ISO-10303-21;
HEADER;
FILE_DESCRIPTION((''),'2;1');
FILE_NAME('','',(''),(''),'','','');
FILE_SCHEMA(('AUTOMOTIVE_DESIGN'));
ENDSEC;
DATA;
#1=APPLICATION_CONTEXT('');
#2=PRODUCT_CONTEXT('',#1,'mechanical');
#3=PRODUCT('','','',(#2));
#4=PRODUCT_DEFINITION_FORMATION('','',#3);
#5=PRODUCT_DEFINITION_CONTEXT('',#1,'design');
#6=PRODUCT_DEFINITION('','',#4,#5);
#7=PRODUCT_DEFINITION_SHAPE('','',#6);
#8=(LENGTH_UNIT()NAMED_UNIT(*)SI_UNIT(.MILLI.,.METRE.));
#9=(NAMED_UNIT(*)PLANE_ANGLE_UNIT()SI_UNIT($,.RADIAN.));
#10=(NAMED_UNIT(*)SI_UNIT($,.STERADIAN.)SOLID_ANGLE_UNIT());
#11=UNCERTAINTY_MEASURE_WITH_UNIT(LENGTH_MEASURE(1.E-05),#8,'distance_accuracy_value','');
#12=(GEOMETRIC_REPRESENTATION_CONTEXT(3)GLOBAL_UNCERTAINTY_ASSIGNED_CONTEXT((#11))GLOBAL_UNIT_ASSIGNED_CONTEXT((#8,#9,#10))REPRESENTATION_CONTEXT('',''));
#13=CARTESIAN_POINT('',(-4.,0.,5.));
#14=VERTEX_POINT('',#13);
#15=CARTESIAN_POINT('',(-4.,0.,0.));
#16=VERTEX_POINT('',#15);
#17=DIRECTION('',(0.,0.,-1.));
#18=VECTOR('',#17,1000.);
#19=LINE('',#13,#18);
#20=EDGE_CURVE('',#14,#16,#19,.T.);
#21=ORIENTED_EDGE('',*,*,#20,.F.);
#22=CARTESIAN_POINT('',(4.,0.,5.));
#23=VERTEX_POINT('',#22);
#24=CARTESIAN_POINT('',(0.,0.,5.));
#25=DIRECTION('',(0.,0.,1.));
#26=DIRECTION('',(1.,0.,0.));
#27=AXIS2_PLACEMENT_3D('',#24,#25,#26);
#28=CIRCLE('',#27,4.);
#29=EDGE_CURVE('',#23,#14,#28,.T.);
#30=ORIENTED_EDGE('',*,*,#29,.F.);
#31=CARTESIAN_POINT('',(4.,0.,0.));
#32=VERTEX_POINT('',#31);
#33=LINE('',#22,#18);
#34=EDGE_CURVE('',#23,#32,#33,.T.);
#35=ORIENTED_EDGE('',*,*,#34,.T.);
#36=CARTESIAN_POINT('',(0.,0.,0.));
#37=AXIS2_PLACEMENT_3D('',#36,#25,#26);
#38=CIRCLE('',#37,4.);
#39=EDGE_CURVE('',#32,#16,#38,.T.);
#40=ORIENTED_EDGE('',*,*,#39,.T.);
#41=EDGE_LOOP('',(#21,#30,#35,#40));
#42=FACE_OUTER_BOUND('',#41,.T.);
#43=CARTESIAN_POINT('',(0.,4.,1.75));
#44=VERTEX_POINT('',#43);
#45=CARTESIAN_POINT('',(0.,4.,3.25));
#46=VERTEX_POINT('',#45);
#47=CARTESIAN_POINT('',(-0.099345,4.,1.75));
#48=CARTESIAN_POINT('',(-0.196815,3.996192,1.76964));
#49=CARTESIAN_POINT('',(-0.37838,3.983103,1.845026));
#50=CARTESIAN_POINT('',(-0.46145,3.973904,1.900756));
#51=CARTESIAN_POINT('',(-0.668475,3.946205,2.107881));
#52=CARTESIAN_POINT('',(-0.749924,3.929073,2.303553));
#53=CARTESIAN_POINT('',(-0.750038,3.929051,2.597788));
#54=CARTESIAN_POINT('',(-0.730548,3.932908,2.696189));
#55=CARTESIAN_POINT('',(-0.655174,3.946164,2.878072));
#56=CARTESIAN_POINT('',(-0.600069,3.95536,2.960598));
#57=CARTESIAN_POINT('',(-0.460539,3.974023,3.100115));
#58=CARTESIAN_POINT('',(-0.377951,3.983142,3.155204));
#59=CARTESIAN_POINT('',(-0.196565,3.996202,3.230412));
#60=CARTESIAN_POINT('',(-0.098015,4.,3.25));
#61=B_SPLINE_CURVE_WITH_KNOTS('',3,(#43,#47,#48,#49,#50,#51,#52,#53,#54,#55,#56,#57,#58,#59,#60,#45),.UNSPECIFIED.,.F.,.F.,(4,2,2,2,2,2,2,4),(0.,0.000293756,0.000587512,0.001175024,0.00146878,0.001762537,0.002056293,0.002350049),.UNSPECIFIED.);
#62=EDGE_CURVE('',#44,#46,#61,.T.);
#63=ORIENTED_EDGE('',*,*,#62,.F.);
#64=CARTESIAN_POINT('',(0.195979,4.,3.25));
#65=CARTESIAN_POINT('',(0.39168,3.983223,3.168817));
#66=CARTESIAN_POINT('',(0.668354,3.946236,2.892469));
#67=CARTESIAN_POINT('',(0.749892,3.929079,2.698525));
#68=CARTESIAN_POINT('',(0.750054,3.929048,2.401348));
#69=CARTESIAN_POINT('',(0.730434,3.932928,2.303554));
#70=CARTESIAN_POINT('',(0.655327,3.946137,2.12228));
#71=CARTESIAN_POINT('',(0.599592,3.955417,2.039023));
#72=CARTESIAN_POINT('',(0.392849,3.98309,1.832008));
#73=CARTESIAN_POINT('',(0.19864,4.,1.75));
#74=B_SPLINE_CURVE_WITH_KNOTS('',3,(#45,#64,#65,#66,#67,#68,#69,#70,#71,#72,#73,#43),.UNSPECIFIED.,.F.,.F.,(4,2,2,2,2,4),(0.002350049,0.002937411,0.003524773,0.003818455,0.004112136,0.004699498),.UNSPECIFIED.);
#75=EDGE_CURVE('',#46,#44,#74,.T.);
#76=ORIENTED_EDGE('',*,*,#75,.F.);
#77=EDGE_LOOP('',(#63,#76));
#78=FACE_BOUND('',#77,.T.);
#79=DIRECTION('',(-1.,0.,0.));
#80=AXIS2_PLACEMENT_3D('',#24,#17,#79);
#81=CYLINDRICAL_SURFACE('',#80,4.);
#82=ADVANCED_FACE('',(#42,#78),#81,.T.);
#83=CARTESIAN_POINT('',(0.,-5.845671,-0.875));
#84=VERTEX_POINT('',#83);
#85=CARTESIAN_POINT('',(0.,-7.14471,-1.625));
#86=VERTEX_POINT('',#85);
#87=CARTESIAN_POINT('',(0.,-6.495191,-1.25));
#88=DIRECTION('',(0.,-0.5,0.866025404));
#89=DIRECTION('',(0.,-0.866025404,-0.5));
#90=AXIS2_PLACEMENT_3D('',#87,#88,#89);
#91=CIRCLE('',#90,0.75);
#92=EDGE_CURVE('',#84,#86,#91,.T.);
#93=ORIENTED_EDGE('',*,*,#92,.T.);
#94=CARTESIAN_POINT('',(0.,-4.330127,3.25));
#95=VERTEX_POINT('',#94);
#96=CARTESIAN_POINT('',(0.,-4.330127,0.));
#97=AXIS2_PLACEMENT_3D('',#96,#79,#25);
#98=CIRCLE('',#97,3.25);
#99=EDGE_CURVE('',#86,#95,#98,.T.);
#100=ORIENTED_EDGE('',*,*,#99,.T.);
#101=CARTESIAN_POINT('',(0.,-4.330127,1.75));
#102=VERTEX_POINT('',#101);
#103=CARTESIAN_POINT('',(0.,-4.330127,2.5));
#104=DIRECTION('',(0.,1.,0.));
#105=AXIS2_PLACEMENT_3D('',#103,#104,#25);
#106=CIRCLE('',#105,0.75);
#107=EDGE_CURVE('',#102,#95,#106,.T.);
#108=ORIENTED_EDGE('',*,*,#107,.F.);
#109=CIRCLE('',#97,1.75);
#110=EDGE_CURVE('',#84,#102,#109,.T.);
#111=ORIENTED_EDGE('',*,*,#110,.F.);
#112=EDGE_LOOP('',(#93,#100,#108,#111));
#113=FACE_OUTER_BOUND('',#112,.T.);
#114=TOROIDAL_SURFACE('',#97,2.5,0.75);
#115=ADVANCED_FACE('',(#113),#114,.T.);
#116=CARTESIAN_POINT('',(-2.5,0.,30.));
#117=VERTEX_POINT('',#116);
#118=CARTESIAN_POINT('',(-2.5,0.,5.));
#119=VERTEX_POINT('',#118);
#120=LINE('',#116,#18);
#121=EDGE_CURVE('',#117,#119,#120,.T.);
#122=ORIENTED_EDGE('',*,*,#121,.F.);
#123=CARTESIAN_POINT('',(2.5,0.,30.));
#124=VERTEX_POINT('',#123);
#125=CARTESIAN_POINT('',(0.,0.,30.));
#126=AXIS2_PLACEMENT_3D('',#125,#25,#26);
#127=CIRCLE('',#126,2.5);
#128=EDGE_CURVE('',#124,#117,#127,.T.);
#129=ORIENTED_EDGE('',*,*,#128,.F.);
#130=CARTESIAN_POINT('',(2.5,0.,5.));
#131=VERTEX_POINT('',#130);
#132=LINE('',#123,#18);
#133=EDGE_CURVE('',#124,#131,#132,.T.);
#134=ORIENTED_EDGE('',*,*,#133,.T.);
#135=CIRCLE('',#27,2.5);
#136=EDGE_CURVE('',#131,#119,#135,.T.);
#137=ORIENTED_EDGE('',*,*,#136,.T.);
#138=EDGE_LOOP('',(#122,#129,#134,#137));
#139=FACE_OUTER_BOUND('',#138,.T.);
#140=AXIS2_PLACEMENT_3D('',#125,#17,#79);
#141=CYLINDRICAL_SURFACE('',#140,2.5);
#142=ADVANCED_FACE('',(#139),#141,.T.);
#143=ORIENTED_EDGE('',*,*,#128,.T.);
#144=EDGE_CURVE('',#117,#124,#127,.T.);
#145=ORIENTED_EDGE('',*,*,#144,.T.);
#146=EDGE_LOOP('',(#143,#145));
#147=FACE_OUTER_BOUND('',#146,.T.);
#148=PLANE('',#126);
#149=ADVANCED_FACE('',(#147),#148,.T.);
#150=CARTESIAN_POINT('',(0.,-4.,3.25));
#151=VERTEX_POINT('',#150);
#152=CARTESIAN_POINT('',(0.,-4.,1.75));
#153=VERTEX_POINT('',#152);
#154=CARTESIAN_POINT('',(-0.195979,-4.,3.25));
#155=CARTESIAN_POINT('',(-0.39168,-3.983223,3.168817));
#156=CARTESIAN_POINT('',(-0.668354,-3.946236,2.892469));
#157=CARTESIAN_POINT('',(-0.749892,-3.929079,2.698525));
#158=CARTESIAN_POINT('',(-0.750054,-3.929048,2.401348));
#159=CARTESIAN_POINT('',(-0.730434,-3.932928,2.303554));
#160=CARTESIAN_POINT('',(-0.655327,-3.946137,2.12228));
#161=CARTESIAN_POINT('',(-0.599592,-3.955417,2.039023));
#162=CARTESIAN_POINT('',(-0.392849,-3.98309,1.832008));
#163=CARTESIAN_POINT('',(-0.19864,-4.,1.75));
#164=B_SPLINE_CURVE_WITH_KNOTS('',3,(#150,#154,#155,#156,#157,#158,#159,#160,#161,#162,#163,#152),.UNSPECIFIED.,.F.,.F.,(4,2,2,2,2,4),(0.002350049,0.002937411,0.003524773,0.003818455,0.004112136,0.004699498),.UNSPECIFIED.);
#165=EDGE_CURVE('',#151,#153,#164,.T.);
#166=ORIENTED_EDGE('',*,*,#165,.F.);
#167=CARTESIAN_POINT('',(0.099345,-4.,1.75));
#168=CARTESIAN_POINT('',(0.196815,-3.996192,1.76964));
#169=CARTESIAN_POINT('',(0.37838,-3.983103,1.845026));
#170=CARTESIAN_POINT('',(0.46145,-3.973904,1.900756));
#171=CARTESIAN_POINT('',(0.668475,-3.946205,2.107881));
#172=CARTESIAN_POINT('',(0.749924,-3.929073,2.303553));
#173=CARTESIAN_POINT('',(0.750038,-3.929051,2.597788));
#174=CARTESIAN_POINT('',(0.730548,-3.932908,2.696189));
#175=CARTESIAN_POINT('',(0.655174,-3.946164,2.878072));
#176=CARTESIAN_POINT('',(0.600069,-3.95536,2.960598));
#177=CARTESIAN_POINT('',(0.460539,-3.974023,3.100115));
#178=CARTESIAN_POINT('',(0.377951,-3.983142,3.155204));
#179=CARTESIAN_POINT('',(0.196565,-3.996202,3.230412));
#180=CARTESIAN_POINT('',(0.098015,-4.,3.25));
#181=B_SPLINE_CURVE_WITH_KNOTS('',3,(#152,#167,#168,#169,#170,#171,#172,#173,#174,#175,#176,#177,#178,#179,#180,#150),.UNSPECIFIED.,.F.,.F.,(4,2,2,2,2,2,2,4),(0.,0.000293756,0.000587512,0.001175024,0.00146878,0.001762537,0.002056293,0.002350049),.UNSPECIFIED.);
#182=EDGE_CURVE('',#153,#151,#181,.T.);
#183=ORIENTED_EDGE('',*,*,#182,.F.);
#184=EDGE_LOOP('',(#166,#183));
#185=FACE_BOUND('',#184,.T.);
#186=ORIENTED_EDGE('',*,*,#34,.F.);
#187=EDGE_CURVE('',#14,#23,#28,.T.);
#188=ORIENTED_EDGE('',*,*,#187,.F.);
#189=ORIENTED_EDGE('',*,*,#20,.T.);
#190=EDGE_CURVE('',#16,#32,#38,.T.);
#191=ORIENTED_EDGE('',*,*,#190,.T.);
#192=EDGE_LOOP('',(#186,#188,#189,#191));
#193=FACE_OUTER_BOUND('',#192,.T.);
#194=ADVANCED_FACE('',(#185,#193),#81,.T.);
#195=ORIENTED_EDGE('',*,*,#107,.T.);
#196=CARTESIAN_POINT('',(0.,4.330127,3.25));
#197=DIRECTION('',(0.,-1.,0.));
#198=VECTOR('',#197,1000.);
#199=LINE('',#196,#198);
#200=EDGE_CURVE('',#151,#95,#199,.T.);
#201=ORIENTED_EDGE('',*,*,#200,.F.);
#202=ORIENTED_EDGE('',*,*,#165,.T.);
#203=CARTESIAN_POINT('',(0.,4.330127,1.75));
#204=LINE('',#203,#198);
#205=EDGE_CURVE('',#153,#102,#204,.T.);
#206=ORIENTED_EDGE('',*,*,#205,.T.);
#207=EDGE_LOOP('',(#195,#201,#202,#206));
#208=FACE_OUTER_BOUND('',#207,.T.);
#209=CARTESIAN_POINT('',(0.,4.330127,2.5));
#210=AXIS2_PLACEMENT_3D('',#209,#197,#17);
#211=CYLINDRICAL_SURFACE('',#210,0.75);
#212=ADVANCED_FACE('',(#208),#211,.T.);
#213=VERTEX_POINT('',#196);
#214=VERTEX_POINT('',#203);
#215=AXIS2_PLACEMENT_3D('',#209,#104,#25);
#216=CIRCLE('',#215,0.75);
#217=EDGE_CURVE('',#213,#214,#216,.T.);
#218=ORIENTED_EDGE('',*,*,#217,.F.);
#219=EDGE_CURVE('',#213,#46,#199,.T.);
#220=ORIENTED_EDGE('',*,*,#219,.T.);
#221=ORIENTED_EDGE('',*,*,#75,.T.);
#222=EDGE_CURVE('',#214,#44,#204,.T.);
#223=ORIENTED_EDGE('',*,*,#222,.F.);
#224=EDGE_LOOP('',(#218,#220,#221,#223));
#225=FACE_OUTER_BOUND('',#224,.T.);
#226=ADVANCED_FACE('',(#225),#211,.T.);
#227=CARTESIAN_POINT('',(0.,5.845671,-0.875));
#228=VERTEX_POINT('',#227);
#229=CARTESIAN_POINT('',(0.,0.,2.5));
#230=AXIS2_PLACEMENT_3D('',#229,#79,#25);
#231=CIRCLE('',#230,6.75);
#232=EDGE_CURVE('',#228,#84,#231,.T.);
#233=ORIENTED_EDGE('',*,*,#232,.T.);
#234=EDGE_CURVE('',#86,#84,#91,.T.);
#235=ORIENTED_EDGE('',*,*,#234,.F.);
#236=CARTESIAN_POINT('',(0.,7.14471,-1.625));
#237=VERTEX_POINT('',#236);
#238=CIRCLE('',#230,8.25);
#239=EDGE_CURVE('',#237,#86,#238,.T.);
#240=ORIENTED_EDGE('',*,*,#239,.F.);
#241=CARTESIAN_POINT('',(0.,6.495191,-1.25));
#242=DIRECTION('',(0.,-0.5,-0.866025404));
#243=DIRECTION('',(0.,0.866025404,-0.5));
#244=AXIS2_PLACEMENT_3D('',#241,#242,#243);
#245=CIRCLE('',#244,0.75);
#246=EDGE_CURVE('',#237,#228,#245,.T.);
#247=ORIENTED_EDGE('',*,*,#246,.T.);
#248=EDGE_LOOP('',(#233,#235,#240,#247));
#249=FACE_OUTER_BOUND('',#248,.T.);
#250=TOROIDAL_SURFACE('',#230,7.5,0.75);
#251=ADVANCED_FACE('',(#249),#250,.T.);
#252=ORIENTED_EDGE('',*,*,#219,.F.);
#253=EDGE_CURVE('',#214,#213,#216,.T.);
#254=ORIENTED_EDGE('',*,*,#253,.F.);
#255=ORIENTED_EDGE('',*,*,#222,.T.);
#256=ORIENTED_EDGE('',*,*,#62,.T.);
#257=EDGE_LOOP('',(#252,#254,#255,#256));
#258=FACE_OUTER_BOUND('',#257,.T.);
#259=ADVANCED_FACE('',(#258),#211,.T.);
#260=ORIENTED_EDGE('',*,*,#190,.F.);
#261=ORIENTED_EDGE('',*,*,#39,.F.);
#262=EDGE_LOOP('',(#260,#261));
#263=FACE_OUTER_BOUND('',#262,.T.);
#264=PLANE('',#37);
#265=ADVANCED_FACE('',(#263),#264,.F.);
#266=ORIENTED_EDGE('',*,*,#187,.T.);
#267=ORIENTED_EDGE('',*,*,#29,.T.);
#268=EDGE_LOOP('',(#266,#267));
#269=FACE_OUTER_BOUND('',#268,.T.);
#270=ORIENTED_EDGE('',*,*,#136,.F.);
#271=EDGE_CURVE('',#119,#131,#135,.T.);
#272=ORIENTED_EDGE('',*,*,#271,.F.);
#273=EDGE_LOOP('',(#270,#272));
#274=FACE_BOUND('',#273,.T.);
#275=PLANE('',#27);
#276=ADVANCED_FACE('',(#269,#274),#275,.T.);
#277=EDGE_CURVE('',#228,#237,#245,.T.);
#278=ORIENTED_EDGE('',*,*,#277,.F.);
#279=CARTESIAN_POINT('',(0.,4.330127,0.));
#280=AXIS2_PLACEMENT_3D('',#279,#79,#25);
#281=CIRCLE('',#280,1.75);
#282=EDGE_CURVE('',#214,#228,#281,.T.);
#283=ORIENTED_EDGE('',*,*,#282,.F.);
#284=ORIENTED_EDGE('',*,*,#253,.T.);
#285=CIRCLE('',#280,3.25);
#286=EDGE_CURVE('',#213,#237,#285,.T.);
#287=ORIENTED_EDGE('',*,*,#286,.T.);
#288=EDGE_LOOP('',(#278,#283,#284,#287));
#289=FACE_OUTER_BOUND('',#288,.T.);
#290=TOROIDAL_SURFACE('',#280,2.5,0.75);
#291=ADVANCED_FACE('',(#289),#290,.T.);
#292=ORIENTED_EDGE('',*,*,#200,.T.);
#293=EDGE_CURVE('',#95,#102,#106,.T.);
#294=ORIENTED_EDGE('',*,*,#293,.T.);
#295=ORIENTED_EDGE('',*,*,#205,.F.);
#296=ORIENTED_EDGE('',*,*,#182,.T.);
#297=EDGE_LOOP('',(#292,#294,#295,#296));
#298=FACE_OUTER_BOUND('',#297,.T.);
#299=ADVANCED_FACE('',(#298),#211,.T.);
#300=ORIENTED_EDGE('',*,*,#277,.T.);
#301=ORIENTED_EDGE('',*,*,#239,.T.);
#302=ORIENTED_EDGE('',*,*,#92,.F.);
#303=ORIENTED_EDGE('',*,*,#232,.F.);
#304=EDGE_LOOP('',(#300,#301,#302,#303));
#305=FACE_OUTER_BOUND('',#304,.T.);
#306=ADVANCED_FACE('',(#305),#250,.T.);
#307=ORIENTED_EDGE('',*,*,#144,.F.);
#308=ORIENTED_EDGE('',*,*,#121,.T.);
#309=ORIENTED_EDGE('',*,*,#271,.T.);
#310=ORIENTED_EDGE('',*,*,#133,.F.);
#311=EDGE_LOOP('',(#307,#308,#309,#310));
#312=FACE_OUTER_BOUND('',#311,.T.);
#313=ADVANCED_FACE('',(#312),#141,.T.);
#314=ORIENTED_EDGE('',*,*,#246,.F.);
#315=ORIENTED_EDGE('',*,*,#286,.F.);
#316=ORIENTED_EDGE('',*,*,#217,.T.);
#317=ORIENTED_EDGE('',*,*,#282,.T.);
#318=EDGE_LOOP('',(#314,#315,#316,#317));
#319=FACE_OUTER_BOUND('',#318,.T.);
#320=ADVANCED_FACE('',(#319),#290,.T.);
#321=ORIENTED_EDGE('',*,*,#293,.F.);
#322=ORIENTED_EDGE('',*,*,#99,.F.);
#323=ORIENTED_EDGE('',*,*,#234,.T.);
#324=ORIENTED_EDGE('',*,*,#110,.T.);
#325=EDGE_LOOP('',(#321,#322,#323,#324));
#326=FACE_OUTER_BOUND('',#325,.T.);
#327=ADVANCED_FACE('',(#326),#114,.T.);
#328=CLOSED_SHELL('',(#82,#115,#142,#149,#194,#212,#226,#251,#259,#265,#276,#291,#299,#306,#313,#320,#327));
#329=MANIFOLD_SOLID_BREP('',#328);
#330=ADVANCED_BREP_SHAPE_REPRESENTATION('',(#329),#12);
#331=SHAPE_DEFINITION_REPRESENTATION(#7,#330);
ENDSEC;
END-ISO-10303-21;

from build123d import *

# Parameters (mm, degrees)
SKETCH1_R           = 4
BOSS_EXTRUDE1_DEPTH = 5
SKETCH2_R           = 2.5
BOSS_EXTRUDE2_DEPTH = 25
SKETCH3_R           = 0.75


with BuildPart() as part:
    # Sketch1 → Boss-Extrude1 (new body)
    with BuildSketch(Plane.XY):
        Circle(SKETCH1_R)
    extrude(amount=BOSS_EXTRUDE1_DEPTH)

    # Sketch2 → Boss-Extrude2 (add)
    with BuildSketch(Plane.XY.offset(5)):
        Circle(SKETCH2_R)
    extrude(amount=BOSS_EXTRUDE2_DEPTH)

    # Sweep1: sweep along a path in Sketch4
    with BuildLine(Plane(origin=(0, 0, 0), x_dir=(0, 0, -1), z_dir=(1, 0, 0))) as sweep1_path:
        Line((-2.5, 0), (-2.5, -4.330127019))
        ThreePointArc((-2.5, -4.330127019), (-1.25, -6.495190528), (1.25, -6.495190528))
        ThreePointArc((1.25, -6.495190528), (5, 0), (1.25, 6.495190528))
        ThreePointArc((1.25, 6.495190528), (-1.25, 6.495190528), (-2.5, 4.330127019))
        Line((-2.5, 4.330127019), (-2.5, 0))
    # Sketch3 → Sweep1 (sweep)
    with BuildSketch(Plane(origin=(0, 0, 0), x_dir=(1, 0, 0), z_dir=(0, 1, 0))):
        with Locations((0, -2.5)):
            Circle(SKETCH3_R)
    sweep(path=sweep1_path.line)


solid = part.part
